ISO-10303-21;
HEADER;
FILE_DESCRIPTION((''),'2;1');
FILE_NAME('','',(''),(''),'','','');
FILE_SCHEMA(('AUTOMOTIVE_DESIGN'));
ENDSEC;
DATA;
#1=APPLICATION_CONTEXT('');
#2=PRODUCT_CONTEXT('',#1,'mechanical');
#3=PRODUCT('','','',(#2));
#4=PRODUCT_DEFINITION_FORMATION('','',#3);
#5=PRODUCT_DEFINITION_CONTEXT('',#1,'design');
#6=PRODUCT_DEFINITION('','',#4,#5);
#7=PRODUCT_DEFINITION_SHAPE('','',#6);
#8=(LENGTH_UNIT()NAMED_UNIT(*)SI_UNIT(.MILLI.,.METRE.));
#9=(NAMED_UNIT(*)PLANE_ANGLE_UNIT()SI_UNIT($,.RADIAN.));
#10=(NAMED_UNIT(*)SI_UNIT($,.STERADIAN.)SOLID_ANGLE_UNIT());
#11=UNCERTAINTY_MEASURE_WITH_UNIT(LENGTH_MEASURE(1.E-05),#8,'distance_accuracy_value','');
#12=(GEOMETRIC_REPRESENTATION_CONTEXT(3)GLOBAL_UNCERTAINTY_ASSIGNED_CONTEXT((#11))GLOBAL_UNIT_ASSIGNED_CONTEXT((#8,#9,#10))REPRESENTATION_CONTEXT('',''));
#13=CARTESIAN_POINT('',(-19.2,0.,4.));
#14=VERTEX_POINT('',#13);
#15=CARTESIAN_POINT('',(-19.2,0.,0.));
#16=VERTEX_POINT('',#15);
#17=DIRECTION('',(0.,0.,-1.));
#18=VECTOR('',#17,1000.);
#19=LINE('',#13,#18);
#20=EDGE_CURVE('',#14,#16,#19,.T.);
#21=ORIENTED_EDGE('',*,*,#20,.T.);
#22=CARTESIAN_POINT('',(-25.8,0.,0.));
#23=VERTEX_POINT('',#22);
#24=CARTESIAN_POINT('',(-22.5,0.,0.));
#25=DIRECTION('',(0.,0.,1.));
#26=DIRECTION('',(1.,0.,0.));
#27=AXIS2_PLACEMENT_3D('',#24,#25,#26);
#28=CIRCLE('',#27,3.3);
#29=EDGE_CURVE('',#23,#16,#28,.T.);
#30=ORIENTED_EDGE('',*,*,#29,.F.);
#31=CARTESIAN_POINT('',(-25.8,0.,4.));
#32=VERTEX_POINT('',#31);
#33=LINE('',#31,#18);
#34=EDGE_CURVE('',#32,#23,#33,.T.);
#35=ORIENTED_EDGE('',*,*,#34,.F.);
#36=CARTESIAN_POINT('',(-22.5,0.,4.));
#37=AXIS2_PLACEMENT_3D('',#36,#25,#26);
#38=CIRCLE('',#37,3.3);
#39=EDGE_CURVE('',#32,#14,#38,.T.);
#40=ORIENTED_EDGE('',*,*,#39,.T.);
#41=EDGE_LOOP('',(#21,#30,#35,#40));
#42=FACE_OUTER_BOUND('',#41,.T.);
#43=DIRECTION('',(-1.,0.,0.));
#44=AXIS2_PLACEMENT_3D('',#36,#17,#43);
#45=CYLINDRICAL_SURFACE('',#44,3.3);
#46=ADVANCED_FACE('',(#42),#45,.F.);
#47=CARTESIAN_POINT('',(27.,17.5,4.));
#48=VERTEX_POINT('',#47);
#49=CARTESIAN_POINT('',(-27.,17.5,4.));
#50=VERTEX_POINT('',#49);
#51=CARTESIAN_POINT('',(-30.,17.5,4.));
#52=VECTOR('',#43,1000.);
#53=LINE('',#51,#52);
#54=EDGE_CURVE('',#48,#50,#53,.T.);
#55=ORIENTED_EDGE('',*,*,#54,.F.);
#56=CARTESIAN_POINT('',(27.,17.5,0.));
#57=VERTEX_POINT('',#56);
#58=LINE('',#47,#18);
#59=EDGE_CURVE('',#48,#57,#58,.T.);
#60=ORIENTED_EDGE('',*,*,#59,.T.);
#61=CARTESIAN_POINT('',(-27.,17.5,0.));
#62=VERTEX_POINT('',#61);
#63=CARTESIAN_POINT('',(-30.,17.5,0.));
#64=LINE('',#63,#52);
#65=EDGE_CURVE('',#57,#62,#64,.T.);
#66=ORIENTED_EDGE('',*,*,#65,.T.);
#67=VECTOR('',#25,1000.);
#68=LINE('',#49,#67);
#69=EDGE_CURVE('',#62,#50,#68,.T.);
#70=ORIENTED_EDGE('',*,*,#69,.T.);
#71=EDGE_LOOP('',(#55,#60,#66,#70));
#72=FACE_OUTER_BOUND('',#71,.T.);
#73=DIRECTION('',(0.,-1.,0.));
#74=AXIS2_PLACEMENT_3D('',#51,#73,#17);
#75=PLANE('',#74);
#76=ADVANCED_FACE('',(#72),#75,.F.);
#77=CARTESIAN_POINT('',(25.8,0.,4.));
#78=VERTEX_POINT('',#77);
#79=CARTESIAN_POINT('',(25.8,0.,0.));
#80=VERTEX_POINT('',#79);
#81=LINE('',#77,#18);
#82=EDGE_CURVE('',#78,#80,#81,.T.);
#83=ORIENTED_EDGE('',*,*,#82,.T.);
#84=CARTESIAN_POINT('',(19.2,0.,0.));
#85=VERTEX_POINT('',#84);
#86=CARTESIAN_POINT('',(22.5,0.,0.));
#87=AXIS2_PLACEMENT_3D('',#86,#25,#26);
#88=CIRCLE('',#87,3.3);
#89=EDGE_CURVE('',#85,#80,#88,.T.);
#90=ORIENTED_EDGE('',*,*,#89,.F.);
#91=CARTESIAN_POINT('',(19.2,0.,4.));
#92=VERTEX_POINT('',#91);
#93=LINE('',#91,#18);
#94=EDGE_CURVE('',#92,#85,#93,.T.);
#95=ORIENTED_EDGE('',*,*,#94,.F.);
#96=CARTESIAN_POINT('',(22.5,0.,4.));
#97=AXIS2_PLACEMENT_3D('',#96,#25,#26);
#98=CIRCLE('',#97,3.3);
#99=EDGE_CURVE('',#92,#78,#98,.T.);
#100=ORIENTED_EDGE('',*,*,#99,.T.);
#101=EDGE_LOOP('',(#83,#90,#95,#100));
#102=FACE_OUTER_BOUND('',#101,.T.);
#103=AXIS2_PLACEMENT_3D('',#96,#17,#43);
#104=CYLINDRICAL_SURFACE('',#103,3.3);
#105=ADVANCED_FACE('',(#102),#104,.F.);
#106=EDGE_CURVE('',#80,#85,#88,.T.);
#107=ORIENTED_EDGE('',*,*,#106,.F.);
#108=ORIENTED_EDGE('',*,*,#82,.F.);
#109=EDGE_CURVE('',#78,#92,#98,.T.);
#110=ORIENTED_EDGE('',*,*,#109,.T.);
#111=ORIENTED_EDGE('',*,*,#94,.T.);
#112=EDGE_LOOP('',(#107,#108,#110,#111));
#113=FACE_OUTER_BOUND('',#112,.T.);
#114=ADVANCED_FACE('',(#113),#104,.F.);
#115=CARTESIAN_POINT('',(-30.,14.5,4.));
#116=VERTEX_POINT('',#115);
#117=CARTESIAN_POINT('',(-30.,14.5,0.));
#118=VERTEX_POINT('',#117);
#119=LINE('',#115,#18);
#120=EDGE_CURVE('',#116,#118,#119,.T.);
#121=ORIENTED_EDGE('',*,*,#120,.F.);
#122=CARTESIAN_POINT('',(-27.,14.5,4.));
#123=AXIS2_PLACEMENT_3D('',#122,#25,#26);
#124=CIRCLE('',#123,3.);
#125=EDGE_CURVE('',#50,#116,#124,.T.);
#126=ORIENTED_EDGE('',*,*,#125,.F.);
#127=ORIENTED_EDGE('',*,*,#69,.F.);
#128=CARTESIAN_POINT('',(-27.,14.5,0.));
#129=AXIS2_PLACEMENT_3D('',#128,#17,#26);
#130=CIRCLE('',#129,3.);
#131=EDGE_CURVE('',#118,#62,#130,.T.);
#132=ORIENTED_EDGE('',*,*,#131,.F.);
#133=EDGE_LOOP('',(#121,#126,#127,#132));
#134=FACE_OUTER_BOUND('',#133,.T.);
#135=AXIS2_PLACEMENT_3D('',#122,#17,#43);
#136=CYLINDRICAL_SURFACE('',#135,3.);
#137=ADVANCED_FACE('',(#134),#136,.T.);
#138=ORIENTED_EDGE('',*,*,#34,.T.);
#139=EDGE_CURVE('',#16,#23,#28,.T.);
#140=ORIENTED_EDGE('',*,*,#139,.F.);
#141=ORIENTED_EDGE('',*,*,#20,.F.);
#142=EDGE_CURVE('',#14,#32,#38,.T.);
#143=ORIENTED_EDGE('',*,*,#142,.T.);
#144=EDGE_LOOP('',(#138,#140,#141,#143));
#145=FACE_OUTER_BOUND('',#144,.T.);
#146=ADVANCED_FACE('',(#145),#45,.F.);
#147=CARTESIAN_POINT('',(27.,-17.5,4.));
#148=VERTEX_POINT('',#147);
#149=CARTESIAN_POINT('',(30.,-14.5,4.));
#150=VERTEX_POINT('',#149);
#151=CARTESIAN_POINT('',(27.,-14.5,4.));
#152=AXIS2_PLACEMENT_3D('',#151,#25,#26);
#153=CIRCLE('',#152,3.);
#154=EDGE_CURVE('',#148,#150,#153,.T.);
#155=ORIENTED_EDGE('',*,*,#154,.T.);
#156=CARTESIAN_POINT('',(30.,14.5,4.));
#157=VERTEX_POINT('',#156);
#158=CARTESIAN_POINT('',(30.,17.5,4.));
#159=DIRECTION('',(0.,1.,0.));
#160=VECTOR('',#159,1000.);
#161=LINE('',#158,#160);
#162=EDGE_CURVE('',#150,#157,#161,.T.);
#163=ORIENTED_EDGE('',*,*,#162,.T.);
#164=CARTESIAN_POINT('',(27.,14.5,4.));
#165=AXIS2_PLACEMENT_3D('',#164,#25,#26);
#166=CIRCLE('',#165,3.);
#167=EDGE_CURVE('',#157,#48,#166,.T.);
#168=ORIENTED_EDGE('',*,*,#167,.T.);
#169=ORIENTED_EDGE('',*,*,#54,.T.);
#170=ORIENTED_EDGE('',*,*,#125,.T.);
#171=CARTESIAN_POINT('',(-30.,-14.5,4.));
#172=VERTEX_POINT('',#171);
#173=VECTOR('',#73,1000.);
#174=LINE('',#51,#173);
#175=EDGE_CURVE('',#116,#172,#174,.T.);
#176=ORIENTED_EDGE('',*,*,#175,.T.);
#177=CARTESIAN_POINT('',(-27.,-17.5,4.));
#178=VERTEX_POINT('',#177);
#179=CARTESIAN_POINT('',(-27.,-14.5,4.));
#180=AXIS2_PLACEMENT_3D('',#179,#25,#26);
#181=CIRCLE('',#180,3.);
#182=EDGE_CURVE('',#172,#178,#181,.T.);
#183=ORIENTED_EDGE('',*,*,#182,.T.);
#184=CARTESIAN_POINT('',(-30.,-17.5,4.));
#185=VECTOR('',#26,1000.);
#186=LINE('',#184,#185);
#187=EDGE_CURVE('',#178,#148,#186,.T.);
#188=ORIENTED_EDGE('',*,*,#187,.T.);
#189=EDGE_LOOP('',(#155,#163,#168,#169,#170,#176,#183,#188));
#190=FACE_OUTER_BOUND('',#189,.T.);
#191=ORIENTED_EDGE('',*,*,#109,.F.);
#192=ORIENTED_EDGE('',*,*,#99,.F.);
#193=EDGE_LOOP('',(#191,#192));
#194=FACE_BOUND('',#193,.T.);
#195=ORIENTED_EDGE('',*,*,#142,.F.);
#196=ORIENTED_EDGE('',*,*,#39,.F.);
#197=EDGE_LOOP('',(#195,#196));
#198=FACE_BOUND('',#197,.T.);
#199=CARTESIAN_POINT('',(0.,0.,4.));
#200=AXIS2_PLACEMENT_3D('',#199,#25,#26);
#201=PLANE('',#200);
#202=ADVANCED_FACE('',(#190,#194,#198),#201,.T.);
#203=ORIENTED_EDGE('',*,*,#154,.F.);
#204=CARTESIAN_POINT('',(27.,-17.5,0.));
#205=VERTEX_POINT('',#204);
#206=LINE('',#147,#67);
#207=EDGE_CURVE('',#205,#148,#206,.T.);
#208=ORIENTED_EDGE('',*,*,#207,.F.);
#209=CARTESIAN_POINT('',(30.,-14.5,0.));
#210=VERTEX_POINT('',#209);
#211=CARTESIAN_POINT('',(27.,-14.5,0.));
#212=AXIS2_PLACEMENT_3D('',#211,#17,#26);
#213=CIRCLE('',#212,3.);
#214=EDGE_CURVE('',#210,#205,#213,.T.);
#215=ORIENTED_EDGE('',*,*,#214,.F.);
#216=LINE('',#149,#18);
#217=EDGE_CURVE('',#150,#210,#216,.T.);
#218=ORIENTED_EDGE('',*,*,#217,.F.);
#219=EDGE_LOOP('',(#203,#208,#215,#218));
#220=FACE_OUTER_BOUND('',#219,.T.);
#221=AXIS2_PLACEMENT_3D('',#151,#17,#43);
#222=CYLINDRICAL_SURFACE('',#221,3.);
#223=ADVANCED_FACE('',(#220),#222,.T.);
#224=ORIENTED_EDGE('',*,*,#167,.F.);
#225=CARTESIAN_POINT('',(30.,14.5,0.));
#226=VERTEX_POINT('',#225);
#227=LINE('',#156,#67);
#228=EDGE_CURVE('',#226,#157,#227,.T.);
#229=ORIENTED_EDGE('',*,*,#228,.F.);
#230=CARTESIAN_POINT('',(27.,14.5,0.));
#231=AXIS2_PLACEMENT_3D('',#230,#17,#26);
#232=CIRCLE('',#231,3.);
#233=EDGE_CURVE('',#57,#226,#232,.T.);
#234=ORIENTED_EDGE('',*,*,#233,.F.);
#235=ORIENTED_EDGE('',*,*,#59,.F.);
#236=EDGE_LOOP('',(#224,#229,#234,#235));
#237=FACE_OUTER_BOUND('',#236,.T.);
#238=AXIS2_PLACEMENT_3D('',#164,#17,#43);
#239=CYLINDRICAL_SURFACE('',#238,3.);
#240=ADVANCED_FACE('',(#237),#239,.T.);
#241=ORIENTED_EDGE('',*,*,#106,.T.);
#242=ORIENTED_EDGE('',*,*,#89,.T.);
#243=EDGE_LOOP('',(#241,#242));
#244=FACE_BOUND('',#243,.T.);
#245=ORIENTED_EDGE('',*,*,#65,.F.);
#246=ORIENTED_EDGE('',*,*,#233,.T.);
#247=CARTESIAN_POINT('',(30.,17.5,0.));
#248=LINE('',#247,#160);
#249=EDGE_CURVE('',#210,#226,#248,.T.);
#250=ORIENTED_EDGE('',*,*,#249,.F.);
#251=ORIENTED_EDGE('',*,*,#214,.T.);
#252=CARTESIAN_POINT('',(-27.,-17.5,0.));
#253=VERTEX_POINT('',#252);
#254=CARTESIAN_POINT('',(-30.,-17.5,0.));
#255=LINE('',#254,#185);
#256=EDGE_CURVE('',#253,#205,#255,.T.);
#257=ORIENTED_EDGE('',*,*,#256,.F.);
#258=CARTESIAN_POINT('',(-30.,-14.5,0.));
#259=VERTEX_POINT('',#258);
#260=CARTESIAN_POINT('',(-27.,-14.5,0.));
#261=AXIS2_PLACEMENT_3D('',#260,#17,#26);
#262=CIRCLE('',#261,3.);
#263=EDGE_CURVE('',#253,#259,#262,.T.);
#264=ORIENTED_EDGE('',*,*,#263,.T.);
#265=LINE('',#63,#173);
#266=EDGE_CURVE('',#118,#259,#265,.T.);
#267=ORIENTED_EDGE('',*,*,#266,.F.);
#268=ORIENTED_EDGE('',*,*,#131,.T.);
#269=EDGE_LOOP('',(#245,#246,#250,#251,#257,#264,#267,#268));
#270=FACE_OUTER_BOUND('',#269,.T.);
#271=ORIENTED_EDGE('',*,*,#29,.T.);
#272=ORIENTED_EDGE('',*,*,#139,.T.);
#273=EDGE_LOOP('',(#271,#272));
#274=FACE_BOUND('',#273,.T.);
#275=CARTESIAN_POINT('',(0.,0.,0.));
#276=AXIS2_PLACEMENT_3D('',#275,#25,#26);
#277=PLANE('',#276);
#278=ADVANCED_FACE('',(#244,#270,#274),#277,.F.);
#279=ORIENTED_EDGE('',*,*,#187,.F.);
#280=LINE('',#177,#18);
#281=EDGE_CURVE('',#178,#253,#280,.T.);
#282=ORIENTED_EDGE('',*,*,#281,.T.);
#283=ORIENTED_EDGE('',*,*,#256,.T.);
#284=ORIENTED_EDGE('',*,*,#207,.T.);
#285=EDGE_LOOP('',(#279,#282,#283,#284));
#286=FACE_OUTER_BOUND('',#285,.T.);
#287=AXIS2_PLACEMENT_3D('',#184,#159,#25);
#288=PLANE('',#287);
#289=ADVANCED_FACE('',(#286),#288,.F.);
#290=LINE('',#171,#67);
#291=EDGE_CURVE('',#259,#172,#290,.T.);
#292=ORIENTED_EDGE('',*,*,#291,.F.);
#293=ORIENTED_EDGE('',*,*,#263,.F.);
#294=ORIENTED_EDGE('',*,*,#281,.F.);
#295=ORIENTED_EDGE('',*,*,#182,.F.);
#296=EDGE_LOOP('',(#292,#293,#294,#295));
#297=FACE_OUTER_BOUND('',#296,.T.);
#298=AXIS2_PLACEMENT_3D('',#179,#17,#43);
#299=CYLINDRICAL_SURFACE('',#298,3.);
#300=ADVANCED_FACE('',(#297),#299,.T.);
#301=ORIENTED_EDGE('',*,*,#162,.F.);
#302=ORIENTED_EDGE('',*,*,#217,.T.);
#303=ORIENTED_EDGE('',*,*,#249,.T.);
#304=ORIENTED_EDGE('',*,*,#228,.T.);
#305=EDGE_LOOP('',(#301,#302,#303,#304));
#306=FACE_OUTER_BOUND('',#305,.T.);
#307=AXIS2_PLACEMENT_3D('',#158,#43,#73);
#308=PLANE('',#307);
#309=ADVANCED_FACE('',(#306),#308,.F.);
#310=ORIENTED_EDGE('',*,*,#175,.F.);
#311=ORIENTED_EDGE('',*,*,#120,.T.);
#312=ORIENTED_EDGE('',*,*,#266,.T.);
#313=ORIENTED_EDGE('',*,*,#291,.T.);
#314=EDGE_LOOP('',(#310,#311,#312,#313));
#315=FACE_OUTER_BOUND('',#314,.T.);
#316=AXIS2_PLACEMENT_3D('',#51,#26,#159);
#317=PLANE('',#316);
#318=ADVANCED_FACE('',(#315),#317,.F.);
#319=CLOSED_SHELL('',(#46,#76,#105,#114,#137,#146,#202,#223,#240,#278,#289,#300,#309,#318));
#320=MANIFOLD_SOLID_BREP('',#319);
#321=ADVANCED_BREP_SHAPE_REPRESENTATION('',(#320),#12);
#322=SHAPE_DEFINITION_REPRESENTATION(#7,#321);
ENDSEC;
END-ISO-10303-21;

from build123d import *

# Parameters (mm, degrees)
SKETCH_1_W      = 60
SKETCH_1_H      = 35
SKETCH_1_R      = 3.3
EXTRUDE_1_DEPTH = 4
FILLET_1_R      = 3


with BuildPart() as part:
    # 草图1 → 凸台-拉伸1 (new body)
    with BuildSketch(Plane.XY):
        Rectangle(SKETCH_1_W, SKETCH_1_H)
        with Locations((-22.5, 0)):
            Circle(SKETCH_1_R, mode=Mode.SUBTRACT)
        with Locations((22.5, 0)):
            Circle(SKETCH_1_R, mode=Mode.SUBTRACT)
    extrude(amount=EXTRUDE_1_DEPTH)

    # 圆角1
    fillet_1_edges = [part.edges().sort_by_distance(p)[0] for p in [
        (30, -17.5, 2),
        (-30, -17.5, 2),
        (-30, 17.5, 2),
        (30, 17.5, 2),
    ]]
    fillet(fillet_1_edges, radius=FILLET_1_R)


solid = part.part
